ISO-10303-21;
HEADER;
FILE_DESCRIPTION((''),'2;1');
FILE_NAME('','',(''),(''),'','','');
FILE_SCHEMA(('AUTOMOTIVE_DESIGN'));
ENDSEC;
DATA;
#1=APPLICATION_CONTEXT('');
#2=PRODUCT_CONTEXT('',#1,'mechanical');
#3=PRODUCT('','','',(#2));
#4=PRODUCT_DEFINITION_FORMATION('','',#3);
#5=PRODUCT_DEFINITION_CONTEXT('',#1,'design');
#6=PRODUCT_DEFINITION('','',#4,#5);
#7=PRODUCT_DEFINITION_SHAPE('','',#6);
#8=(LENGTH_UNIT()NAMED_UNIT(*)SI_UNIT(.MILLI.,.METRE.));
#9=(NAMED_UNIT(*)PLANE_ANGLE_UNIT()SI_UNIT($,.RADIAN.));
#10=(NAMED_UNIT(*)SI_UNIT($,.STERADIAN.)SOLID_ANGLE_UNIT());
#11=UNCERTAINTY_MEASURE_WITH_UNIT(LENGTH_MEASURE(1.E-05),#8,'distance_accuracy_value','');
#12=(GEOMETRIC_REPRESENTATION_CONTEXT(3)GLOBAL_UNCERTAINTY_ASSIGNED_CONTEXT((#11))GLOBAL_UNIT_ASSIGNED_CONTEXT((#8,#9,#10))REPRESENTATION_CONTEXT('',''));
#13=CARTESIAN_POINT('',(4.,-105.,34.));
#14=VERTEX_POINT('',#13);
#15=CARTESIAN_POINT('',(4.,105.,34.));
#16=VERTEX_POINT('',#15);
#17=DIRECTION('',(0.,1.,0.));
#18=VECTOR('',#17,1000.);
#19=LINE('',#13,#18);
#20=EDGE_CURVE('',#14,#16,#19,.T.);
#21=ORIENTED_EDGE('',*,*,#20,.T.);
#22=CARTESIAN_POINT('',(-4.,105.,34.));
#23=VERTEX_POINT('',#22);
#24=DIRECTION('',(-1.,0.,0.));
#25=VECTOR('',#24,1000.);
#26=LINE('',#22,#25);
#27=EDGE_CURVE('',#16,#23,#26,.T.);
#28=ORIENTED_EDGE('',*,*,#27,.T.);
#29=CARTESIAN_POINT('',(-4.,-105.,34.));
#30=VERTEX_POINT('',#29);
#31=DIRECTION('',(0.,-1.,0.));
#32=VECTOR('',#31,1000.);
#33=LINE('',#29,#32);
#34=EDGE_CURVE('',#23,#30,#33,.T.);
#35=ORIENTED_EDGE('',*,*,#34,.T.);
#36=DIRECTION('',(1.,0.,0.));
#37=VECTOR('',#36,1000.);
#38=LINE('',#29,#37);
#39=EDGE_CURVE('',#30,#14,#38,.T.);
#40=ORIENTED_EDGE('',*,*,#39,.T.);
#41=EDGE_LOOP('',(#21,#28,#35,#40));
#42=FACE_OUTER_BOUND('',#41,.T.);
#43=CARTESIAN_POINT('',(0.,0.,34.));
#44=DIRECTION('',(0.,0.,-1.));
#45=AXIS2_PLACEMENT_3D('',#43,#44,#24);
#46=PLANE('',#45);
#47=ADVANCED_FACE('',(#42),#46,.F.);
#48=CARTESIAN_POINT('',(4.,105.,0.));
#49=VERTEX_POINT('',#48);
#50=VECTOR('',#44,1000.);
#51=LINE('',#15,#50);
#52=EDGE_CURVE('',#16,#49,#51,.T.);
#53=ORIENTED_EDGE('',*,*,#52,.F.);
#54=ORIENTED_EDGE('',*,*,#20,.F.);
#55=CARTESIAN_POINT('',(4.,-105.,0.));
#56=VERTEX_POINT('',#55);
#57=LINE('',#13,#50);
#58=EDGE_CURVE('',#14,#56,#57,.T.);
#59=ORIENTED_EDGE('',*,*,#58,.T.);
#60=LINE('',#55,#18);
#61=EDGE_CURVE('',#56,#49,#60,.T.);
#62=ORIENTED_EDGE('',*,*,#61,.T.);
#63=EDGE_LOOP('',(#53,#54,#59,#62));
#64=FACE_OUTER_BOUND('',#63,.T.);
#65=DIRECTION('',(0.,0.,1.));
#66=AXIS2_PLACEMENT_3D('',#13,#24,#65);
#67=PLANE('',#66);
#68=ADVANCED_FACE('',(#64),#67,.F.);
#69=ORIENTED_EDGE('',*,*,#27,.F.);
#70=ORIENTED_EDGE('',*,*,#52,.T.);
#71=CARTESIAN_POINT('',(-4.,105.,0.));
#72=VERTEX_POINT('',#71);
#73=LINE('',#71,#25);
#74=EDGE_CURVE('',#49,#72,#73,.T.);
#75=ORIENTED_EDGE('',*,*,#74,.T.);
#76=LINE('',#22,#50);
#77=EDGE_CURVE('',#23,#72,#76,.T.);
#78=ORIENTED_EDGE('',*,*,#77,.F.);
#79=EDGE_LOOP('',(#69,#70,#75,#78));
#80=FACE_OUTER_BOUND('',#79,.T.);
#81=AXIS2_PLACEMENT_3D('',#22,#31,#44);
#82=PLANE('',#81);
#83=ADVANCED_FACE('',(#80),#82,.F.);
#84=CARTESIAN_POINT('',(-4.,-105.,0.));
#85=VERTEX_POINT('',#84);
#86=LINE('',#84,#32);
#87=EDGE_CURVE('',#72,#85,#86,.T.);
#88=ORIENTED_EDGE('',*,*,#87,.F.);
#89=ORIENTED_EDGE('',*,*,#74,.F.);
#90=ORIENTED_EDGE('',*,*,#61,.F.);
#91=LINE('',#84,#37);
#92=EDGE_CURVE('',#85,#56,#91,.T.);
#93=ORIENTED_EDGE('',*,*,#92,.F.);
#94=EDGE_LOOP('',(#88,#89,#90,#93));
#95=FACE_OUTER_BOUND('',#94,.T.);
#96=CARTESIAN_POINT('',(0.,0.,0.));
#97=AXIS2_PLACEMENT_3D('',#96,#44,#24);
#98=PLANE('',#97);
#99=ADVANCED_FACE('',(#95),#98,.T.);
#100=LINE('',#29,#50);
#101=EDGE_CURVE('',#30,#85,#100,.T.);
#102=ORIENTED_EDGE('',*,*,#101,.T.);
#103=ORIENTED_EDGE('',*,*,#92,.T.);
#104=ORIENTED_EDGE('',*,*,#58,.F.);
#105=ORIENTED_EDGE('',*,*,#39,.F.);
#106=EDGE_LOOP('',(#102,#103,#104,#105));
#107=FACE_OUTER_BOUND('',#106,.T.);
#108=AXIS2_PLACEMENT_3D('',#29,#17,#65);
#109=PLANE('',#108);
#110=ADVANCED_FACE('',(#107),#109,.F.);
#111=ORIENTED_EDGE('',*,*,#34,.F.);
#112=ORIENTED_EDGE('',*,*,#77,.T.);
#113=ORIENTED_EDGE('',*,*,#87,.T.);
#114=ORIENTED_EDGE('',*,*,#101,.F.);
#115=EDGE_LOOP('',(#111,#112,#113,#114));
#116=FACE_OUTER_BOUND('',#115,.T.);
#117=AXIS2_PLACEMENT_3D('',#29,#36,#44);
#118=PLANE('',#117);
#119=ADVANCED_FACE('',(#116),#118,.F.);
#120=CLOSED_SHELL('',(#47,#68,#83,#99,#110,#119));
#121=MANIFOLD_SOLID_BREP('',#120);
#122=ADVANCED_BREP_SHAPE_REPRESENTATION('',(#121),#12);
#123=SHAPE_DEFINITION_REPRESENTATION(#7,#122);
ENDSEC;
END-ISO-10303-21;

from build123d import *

# Parameters (mm, degrees)
SKETCH_1_W      = 8
SKETCH_1_H      = 210
EXTRUDE_1_DEPTH = 34


with BuildPart() as part:
    # 草图1 → 凸台-拉伸1 (new body)
    with BuildSketch(Plane.XY):
        Rectangle(SKETCH_1_W, SKETCH_1_H)
    extrude(amount=EXTRUDE_1_DEPTH)


solid = part.part
